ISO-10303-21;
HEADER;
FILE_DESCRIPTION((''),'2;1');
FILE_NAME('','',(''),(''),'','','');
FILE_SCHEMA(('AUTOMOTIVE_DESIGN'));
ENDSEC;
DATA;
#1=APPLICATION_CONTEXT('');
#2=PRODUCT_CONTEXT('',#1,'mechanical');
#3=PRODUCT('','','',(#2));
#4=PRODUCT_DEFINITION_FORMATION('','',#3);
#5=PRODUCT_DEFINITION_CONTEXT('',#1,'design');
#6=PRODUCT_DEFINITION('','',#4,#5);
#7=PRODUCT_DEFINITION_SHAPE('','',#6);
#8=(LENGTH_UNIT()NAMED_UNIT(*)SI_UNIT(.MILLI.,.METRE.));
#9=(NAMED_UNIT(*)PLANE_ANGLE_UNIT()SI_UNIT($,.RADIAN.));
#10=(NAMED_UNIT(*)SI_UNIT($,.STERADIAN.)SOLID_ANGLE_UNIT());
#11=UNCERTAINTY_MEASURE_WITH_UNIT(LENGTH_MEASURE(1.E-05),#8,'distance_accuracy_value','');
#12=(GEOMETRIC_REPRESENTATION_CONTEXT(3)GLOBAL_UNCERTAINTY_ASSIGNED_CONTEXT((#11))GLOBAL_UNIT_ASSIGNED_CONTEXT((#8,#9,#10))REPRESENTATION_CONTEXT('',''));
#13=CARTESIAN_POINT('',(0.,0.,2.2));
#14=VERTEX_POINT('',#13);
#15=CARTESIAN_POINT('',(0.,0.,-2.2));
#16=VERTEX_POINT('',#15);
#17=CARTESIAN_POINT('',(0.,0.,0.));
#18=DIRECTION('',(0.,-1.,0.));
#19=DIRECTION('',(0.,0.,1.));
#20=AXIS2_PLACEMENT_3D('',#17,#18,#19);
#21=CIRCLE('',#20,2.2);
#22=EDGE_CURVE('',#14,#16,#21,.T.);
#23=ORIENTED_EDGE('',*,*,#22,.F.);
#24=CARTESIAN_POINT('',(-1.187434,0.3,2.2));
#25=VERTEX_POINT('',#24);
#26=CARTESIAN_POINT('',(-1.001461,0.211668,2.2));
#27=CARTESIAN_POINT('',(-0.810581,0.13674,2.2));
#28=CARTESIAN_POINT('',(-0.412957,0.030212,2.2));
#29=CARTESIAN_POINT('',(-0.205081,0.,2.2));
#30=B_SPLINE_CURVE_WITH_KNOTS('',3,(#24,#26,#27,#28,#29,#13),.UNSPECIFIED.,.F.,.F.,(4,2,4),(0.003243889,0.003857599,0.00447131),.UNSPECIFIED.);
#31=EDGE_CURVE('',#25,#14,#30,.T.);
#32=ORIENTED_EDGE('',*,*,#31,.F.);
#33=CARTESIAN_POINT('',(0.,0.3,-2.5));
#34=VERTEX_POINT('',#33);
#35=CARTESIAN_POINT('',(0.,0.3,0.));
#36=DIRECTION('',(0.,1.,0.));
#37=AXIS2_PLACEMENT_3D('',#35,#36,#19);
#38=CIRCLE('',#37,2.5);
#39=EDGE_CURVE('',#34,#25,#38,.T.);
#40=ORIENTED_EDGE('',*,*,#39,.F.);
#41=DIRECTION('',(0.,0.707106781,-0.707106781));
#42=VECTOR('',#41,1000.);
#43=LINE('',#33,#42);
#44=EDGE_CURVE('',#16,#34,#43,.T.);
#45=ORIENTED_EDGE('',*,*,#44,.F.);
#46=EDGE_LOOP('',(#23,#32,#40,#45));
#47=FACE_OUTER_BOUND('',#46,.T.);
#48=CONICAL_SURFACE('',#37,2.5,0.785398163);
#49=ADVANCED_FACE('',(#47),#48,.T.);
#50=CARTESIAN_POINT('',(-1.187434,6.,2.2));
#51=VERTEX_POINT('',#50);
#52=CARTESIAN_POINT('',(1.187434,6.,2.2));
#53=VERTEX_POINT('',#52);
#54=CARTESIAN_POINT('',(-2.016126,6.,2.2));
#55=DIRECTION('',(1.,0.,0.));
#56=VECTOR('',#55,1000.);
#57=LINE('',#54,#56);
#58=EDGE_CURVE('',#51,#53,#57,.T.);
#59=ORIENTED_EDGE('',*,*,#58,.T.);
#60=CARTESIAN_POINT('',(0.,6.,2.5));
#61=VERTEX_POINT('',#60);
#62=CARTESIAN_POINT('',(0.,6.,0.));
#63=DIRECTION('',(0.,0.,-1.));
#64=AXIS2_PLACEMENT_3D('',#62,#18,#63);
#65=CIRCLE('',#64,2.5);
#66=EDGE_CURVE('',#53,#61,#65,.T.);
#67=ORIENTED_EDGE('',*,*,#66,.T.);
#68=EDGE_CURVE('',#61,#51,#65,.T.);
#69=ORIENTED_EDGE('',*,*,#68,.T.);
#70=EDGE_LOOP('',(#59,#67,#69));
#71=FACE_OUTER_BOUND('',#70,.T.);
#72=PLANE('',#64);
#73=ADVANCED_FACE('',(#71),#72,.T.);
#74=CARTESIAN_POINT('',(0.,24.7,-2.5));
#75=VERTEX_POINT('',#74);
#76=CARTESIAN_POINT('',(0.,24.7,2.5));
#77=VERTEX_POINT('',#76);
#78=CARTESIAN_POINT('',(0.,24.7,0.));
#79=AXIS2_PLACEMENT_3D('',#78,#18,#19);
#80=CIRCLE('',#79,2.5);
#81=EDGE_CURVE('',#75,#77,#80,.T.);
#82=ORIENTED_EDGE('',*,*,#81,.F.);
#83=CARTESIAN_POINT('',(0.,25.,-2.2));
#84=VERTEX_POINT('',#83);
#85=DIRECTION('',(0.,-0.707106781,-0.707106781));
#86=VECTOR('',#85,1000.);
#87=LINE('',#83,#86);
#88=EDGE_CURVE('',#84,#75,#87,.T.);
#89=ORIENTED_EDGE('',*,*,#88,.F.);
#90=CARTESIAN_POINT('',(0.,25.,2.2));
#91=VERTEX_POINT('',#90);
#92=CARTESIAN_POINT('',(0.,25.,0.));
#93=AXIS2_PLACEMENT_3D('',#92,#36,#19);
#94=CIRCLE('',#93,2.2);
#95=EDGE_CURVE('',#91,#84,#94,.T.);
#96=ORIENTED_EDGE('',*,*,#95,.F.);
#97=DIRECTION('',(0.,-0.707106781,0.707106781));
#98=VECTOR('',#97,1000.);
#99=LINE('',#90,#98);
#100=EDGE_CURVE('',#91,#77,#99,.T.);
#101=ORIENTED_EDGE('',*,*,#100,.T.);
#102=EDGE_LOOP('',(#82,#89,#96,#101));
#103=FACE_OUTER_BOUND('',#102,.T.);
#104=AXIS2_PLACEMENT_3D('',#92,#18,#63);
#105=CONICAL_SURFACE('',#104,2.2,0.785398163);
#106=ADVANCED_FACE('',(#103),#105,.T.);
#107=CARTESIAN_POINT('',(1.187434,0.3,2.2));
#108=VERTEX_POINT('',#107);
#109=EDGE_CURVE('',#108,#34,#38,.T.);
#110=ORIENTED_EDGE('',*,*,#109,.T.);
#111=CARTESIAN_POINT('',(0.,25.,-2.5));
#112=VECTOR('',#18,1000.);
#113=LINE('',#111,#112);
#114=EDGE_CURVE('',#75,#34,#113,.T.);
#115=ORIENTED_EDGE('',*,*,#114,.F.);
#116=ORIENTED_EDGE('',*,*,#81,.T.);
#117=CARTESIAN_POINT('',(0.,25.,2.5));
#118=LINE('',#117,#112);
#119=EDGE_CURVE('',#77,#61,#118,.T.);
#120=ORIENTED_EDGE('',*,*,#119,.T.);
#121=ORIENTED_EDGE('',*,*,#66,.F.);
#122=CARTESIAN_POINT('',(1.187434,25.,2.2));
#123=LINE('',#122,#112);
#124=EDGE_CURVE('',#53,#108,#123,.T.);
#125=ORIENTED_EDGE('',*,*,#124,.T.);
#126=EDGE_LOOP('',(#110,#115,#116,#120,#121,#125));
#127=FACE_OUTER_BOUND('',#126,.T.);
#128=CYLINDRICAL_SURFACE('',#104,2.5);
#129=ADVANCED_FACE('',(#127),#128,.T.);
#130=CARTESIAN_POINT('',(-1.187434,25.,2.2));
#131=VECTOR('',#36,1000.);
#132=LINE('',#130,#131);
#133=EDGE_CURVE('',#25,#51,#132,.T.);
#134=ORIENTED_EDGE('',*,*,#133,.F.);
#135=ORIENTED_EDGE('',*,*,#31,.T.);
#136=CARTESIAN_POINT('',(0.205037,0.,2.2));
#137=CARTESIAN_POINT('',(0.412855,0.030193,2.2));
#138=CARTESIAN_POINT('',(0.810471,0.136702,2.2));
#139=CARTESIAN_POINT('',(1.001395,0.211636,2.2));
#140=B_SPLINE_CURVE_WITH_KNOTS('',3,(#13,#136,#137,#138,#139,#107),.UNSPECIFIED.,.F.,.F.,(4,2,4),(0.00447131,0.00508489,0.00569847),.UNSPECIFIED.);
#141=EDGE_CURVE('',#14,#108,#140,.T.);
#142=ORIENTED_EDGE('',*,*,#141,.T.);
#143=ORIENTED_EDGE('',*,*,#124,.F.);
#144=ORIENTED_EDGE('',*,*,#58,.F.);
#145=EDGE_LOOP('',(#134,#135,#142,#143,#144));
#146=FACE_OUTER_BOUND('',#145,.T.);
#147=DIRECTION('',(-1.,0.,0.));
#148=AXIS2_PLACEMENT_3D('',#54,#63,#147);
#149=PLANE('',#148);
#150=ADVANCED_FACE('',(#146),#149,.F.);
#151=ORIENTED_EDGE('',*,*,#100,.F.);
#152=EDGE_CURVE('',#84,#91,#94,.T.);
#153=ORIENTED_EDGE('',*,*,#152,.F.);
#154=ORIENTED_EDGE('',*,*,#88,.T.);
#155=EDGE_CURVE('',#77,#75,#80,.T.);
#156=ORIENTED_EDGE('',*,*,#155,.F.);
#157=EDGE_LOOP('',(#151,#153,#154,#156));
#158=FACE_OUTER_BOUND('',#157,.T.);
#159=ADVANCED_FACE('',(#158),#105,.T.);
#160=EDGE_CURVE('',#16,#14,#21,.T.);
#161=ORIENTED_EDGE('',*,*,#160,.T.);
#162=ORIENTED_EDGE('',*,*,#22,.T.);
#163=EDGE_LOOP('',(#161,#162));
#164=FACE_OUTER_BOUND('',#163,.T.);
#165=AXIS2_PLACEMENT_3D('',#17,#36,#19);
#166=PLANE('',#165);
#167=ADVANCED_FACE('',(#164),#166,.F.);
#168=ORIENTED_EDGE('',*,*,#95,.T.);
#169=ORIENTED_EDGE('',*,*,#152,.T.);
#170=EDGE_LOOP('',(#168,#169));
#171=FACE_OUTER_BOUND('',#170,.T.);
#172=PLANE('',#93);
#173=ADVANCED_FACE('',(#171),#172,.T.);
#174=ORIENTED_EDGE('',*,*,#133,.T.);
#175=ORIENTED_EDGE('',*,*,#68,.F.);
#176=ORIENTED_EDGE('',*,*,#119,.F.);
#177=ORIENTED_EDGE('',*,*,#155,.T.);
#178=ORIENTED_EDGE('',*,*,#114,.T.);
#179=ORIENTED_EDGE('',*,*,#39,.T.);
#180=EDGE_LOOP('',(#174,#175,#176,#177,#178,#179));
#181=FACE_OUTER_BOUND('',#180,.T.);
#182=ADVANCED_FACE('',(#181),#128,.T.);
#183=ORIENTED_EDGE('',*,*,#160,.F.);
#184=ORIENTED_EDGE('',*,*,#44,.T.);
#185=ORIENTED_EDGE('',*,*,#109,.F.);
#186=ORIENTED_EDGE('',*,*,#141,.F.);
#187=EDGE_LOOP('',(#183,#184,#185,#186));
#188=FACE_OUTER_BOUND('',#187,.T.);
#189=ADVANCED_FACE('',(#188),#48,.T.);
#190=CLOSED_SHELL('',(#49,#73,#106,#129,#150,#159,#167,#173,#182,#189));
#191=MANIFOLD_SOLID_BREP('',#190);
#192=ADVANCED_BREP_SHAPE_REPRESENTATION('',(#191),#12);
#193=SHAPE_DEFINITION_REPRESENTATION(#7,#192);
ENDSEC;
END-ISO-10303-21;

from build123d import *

# Parameters (mm, degrees)
SKETCH1_R           = 2.5
BOSS_EXTRUDE1_DEPTH = 25
CHAMFER1_SIZE       = 0.3
SKETCH3_W           = 4.032252552
SKETCH3_H           = 0.6
CUT_EXTRUDE2_DEPTH  = 6


with BuildPart() as part:
    # Sketch1 → Boss-Extrude1 (new body)
    with BuildSketch(Plane(origin=(0, 0, 0), x_dir=(1, 0, 0), z_dir=(0, 1, 0))):
        with Locations(Location((0, 0, 0), (0, 0, 270))):
            Circle(SKETCH1_R)
    extrude(amount=BOSS_EXTRUDE1_DEPTH)

    # Chamfer1
    chamfer1_edges = [part.edges().sort_by_distance(p)[0] for p in [
        (0, 0, -2.5),
        (0, 25, -2.5),
    ]]
    chamfer(chamfer1_edges, length=CHAMFER1_SIZE)

    # Sketch3 → Cut-Extrude2 (cut)
    with BuildSketch(Plane.XZ):
        with Locations((0, 2.5)):
            Rectangle(SKETCH3_W, SKETCH3_H)
    extrude(amount=-CUT_EXTRUDE2_DEPTH, mode=Mode.SUBTRACT)


solid = part.part
